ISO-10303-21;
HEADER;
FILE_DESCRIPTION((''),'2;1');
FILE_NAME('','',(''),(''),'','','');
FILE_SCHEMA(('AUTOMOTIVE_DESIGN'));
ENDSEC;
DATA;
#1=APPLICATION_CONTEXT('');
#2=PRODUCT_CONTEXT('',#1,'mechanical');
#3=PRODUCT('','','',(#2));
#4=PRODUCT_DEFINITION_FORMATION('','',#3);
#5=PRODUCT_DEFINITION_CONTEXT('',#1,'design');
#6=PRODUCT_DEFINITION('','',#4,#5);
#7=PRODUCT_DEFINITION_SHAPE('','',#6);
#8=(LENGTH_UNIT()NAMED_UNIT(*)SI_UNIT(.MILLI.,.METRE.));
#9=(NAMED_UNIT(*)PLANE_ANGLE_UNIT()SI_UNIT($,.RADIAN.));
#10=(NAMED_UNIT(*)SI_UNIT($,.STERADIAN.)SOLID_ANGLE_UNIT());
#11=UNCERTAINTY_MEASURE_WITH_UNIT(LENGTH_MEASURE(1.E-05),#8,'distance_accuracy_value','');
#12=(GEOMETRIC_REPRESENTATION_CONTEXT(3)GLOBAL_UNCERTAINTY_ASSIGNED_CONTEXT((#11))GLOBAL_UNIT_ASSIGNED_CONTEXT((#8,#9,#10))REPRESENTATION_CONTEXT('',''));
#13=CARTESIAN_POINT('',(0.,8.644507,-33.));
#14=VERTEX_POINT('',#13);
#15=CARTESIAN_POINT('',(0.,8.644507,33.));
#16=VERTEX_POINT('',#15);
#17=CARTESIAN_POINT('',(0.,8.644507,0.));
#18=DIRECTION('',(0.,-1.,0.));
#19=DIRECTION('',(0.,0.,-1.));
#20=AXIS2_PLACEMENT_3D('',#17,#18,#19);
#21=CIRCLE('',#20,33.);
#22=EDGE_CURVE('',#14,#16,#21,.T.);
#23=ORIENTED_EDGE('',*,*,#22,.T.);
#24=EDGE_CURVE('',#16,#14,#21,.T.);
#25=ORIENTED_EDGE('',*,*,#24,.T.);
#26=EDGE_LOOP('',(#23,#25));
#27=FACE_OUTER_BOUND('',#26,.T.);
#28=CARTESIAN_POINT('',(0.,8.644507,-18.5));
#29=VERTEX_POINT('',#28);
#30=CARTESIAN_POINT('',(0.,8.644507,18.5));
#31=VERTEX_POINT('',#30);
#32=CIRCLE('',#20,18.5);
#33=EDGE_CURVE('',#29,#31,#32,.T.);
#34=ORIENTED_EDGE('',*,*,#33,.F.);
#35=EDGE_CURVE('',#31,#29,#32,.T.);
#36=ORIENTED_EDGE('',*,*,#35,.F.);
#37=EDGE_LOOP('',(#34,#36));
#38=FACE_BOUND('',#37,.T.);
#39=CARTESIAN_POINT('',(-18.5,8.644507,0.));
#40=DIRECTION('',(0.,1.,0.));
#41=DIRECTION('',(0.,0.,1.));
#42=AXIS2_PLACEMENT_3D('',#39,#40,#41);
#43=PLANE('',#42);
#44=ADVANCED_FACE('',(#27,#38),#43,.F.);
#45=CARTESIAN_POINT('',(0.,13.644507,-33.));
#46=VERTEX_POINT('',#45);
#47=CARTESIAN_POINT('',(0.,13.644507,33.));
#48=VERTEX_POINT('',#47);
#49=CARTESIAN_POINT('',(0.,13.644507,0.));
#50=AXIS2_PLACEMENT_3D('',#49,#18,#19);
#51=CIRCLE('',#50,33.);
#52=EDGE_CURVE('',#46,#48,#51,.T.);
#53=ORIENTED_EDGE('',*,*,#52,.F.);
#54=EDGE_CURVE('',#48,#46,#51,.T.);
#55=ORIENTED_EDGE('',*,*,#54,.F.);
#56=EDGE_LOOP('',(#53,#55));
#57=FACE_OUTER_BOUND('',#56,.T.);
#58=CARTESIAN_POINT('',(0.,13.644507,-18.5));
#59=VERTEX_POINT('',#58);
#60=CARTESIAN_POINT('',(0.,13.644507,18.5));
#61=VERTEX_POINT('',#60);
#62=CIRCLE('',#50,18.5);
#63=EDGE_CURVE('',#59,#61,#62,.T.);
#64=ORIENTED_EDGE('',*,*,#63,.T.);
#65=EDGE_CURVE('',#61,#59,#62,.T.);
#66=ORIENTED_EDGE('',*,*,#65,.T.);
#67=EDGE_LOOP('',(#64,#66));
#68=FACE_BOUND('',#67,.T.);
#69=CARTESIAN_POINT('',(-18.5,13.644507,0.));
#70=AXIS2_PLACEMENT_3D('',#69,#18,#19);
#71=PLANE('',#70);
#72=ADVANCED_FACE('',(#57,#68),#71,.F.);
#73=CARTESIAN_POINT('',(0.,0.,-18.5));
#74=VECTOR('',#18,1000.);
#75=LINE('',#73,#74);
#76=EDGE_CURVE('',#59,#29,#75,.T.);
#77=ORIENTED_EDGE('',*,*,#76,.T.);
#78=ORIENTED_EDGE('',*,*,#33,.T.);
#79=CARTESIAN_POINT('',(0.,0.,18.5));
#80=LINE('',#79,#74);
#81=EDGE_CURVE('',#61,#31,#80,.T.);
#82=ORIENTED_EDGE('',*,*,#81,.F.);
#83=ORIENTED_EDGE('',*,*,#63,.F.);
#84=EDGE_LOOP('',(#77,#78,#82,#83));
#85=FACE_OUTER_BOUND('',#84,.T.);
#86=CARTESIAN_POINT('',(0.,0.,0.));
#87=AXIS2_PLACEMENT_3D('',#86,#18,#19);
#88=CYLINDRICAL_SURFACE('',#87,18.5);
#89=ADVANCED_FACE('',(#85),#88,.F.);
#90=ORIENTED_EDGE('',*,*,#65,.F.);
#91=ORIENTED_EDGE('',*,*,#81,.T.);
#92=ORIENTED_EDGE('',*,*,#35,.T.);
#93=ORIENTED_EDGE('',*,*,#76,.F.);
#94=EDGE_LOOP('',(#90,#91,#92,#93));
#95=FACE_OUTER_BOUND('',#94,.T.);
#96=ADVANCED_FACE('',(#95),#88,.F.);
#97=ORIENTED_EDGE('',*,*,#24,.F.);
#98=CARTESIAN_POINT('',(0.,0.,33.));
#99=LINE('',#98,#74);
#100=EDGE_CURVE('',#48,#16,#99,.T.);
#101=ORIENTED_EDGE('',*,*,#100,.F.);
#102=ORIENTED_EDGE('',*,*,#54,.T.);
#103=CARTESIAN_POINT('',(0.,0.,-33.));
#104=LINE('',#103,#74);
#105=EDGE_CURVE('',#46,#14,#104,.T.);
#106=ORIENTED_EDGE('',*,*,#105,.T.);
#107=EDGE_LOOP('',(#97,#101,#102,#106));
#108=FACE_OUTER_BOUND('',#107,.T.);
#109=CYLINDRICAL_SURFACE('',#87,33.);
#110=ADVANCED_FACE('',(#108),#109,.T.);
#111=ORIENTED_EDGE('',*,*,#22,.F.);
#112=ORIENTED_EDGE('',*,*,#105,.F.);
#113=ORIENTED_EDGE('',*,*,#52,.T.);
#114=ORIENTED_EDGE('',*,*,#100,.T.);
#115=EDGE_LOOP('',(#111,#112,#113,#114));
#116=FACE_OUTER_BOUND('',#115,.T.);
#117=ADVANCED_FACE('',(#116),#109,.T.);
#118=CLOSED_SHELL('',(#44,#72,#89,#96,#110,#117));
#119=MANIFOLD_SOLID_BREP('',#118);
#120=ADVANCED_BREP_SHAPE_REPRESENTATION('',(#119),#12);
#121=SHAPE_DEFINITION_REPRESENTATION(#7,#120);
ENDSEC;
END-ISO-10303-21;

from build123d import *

# Parameters (mm, degrees)
SKETCH1_W = 14.5
SKETCH1_H = 5


with BuildPart() as part:
    # Sketch1 → Base-Revolve (revolve)
    with BuildSketch(Plane.XY, mode=Mode.PRIVATE) as base_revolve_sk:
        with Locations((-25.75, 11.144507042)):
            Rectangle(SKETCH1_W, SKETCH1_H)
    revolve(base_revolve_sk.sketch.rotate(Axis((0, 0, 0), (0, 1, 0)), 270), axis=Axis((0, 0, 0), (0, 1, 0)))


solid = part.part
